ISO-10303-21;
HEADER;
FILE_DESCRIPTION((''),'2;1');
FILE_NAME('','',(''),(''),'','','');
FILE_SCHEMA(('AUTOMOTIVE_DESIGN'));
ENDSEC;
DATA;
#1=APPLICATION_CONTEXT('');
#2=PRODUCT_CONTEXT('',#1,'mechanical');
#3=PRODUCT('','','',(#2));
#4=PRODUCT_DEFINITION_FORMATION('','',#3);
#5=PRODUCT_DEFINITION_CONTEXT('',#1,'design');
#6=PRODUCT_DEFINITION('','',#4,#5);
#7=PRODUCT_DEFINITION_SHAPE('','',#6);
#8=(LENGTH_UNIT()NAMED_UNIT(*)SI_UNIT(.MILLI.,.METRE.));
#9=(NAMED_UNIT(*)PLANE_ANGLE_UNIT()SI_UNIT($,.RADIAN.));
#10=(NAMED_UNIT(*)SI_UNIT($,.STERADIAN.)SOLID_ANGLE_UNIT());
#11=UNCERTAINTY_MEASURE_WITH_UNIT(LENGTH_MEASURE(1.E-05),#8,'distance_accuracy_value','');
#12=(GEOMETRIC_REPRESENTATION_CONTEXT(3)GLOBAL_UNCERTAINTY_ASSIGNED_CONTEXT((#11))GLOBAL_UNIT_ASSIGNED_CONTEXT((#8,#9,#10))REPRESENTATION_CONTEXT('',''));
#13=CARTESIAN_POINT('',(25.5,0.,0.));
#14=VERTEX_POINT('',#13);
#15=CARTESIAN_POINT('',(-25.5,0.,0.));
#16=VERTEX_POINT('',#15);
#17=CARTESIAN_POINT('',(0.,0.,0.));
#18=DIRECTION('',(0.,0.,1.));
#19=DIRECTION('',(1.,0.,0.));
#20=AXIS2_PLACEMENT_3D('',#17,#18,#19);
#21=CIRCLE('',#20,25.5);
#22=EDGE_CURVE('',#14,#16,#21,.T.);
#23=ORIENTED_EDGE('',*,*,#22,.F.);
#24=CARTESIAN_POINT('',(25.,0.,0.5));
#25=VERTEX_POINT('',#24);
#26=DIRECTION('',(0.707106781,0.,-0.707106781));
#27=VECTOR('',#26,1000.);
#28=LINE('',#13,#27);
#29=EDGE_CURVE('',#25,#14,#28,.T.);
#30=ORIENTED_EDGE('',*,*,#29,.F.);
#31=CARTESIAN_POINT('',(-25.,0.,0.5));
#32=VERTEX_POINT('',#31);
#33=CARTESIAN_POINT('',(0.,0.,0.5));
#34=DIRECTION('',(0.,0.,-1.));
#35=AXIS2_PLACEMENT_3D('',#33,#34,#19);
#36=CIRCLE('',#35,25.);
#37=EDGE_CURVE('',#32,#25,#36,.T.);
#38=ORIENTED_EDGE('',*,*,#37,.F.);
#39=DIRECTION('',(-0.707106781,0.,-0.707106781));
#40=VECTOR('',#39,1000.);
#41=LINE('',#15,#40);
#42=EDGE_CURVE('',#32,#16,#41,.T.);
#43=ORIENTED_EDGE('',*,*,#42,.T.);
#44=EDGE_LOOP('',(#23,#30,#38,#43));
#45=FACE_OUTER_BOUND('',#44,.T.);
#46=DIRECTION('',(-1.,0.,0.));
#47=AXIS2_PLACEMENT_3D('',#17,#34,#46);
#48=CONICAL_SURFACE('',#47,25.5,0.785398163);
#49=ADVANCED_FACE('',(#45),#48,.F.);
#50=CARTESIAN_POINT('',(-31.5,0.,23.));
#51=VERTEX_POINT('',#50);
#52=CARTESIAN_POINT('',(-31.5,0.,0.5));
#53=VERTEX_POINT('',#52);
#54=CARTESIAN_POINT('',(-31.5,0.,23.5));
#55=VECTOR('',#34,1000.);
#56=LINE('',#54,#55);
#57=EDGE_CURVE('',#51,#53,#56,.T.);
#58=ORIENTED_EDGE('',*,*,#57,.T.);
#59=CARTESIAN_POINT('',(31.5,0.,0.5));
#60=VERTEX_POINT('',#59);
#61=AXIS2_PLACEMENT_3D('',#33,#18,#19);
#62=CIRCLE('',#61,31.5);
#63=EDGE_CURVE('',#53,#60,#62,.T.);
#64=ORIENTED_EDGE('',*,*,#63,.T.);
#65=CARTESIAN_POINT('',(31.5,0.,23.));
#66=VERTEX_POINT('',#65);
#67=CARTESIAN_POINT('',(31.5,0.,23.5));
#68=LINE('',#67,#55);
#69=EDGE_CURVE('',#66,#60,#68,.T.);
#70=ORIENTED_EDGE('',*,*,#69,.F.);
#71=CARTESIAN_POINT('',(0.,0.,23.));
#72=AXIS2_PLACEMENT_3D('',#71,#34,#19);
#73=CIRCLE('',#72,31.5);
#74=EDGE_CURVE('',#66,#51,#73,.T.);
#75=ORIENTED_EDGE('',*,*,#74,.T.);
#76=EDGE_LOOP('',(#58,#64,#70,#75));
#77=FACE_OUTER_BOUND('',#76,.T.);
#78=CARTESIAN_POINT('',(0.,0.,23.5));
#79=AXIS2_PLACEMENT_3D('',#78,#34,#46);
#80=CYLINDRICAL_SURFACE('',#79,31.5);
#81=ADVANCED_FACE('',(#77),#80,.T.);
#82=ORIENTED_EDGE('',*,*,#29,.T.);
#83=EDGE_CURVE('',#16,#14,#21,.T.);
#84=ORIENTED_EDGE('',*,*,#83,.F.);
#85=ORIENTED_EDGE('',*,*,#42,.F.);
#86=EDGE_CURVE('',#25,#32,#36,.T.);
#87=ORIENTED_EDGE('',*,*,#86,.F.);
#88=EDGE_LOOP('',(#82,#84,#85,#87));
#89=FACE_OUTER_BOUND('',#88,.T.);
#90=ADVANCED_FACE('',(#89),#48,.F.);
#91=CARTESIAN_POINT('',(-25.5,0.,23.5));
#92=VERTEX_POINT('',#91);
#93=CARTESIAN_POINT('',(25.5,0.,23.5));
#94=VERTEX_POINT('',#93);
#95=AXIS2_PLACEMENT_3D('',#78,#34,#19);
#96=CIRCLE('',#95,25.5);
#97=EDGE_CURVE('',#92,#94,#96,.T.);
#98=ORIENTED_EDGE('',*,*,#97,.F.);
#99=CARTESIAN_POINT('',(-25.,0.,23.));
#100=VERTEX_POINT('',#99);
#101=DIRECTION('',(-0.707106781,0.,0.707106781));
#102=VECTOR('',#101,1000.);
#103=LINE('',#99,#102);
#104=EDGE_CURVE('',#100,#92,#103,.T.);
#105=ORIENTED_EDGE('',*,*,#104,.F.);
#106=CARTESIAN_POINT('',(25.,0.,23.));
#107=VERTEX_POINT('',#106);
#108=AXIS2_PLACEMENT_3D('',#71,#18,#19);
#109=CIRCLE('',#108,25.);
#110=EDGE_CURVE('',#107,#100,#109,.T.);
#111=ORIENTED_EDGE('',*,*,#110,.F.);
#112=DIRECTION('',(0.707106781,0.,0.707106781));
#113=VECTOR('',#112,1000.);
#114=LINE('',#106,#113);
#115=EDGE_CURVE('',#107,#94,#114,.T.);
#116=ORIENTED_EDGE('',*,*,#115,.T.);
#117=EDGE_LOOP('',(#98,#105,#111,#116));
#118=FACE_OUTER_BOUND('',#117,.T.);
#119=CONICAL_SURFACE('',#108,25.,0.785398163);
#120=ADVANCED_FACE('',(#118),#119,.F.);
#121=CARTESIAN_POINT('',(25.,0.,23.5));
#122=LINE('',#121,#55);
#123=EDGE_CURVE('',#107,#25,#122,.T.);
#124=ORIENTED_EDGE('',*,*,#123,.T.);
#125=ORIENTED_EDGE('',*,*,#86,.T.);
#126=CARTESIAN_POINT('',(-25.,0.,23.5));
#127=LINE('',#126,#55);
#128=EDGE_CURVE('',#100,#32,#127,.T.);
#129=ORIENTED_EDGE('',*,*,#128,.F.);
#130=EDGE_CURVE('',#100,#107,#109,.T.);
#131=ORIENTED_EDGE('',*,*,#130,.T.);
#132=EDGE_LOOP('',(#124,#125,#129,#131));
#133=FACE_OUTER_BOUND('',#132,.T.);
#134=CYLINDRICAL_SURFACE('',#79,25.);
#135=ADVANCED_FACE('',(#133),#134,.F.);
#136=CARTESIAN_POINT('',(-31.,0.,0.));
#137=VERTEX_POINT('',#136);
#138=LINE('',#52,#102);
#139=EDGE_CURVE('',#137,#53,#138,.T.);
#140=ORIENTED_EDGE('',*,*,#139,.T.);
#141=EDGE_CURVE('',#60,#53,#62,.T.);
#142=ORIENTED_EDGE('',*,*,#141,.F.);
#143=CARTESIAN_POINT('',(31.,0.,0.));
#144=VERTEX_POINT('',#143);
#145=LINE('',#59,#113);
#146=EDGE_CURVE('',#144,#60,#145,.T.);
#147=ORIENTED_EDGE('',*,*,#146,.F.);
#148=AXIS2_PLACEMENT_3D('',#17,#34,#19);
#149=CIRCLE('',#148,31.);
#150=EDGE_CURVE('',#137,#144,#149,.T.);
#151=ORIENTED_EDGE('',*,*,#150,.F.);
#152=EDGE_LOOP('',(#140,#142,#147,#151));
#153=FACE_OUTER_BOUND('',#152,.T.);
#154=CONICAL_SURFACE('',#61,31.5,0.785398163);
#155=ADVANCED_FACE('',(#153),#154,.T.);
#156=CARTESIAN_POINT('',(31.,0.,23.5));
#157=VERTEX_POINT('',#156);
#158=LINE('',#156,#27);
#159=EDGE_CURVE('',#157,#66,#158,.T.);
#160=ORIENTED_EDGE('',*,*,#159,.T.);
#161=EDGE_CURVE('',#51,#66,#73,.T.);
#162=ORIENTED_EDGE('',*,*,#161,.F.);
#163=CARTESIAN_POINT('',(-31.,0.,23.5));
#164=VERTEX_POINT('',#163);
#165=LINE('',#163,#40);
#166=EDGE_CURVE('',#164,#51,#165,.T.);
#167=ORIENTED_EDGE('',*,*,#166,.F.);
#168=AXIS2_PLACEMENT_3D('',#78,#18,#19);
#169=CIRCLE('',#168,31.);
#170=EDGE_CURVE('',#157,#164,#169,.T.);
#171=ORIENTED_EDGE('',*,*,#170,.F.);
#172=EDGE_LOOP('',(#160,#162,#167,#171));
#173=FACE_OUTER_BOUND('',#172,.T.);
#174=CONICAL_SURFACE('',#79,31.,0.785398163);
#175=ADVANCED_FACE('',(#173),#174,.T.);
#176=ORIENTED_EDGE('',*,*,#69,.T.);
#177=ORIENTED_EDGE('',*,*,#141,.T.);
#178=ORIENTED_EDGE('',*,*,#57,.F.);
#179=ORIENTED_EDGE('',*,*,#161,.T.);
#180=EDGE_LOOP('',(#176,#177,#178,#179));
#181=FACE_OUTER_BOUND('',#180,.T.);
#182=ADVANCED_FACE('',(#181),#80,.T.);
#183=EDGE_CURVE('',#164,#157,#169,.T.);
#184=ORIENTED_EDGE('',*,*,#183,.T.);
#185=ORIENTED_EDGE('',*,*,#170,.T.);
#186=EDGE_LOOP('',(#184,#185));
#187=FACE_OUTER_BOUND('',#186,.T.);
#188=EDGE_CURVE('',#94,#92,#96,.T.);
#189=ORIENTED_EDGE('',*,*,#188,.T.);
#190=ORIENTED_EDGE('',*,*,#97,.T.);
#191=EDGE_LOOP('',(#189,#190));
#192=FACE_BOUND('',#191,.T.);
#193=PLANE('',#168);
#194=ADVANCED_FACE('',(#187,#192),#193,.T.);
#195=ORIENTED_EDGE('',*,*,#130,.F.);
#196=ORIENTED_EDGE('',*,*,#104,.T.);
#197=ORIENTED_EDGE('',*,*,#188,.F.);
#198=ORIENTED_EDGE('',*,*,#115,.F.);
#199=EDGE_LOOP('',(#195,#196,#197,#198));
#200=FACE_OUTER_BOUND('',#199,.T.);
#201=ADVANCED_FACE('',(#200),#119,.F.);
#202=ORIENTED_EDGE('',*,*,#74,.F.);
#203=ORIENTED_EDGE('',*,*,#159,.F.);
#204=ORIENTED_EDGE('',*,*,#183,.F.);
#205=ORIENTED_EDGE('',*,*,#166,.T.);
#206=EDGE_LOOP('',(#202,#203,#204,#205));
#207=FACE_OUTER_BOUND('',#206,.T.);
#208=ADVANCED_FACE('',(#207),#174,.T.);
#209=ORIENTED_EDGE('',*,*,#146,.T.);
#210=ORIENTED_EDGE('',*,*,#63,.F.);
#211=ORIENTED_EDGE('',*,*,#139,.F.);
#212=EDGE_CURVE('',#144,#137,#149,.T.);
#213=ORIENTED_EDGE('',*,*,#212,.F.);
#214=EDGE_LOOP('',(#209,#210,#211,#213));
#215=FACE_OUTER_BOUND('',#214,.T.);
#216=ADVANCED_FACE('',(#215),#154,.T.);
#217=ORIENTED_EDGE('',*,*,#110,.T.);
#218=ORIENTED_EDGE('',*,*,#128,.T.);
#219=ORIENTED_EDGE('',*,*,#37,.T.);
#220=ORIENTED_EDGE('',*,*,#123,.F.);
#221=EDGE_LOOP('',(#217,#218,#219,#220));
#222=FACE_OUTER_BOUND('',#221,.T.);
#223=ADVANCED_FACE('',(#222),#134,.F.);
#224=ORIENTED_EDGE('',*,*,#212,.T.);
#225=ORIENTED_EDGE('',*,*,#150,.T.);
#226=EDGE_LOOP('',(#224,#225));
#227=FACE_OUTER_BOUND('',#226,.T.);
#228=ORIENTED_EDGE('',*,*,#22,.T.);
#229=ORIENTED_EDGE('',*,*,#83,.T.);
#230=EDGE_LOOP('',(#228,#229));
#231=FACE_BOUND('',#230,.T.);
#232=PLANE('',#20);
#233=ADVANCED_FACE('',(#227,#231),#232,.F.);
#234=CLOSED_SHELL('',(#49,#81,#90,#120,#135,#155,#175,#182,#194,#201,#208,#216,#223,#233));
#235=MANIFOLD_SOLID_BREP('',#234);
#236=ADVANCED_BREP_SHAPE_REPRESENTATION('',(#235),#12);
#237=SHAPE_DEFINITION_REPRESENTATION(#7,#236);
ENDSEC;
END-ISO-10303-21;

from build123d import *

# Parameters (mm, degrees)
SKETCH_1_R      = 31.5
SKETCH_1_R_2    = 25
EXTRUDE_1_DEPTH = 23.5
CHAMFER_1_SIZE  = 0.5


with BuildPart() as part:
    # 草图1 → 凸台-拉伸1 (new body)
    with BuildSketch(Plane.XY):
        Circle(SKETCH_1_R)
        Circle(SKETCH_1_R_2, mode=Mode.SUBTRACT)
    extrude(amount=EXTRUDE_1_DEPTH)

    # 倒角1
    chamfer_1_edges = [part.edges().sort_by_distance(p)[0] for p in [
        (-31.5, 0, 0),
        (-31.5, 0, 23.5),
        (-25, 0, 0),
        (-25, 0, 23.5),
    ]]
    chamfer(chamfer_1_edges, length=CHAMFER_1_SIZE)


solid = part.part
